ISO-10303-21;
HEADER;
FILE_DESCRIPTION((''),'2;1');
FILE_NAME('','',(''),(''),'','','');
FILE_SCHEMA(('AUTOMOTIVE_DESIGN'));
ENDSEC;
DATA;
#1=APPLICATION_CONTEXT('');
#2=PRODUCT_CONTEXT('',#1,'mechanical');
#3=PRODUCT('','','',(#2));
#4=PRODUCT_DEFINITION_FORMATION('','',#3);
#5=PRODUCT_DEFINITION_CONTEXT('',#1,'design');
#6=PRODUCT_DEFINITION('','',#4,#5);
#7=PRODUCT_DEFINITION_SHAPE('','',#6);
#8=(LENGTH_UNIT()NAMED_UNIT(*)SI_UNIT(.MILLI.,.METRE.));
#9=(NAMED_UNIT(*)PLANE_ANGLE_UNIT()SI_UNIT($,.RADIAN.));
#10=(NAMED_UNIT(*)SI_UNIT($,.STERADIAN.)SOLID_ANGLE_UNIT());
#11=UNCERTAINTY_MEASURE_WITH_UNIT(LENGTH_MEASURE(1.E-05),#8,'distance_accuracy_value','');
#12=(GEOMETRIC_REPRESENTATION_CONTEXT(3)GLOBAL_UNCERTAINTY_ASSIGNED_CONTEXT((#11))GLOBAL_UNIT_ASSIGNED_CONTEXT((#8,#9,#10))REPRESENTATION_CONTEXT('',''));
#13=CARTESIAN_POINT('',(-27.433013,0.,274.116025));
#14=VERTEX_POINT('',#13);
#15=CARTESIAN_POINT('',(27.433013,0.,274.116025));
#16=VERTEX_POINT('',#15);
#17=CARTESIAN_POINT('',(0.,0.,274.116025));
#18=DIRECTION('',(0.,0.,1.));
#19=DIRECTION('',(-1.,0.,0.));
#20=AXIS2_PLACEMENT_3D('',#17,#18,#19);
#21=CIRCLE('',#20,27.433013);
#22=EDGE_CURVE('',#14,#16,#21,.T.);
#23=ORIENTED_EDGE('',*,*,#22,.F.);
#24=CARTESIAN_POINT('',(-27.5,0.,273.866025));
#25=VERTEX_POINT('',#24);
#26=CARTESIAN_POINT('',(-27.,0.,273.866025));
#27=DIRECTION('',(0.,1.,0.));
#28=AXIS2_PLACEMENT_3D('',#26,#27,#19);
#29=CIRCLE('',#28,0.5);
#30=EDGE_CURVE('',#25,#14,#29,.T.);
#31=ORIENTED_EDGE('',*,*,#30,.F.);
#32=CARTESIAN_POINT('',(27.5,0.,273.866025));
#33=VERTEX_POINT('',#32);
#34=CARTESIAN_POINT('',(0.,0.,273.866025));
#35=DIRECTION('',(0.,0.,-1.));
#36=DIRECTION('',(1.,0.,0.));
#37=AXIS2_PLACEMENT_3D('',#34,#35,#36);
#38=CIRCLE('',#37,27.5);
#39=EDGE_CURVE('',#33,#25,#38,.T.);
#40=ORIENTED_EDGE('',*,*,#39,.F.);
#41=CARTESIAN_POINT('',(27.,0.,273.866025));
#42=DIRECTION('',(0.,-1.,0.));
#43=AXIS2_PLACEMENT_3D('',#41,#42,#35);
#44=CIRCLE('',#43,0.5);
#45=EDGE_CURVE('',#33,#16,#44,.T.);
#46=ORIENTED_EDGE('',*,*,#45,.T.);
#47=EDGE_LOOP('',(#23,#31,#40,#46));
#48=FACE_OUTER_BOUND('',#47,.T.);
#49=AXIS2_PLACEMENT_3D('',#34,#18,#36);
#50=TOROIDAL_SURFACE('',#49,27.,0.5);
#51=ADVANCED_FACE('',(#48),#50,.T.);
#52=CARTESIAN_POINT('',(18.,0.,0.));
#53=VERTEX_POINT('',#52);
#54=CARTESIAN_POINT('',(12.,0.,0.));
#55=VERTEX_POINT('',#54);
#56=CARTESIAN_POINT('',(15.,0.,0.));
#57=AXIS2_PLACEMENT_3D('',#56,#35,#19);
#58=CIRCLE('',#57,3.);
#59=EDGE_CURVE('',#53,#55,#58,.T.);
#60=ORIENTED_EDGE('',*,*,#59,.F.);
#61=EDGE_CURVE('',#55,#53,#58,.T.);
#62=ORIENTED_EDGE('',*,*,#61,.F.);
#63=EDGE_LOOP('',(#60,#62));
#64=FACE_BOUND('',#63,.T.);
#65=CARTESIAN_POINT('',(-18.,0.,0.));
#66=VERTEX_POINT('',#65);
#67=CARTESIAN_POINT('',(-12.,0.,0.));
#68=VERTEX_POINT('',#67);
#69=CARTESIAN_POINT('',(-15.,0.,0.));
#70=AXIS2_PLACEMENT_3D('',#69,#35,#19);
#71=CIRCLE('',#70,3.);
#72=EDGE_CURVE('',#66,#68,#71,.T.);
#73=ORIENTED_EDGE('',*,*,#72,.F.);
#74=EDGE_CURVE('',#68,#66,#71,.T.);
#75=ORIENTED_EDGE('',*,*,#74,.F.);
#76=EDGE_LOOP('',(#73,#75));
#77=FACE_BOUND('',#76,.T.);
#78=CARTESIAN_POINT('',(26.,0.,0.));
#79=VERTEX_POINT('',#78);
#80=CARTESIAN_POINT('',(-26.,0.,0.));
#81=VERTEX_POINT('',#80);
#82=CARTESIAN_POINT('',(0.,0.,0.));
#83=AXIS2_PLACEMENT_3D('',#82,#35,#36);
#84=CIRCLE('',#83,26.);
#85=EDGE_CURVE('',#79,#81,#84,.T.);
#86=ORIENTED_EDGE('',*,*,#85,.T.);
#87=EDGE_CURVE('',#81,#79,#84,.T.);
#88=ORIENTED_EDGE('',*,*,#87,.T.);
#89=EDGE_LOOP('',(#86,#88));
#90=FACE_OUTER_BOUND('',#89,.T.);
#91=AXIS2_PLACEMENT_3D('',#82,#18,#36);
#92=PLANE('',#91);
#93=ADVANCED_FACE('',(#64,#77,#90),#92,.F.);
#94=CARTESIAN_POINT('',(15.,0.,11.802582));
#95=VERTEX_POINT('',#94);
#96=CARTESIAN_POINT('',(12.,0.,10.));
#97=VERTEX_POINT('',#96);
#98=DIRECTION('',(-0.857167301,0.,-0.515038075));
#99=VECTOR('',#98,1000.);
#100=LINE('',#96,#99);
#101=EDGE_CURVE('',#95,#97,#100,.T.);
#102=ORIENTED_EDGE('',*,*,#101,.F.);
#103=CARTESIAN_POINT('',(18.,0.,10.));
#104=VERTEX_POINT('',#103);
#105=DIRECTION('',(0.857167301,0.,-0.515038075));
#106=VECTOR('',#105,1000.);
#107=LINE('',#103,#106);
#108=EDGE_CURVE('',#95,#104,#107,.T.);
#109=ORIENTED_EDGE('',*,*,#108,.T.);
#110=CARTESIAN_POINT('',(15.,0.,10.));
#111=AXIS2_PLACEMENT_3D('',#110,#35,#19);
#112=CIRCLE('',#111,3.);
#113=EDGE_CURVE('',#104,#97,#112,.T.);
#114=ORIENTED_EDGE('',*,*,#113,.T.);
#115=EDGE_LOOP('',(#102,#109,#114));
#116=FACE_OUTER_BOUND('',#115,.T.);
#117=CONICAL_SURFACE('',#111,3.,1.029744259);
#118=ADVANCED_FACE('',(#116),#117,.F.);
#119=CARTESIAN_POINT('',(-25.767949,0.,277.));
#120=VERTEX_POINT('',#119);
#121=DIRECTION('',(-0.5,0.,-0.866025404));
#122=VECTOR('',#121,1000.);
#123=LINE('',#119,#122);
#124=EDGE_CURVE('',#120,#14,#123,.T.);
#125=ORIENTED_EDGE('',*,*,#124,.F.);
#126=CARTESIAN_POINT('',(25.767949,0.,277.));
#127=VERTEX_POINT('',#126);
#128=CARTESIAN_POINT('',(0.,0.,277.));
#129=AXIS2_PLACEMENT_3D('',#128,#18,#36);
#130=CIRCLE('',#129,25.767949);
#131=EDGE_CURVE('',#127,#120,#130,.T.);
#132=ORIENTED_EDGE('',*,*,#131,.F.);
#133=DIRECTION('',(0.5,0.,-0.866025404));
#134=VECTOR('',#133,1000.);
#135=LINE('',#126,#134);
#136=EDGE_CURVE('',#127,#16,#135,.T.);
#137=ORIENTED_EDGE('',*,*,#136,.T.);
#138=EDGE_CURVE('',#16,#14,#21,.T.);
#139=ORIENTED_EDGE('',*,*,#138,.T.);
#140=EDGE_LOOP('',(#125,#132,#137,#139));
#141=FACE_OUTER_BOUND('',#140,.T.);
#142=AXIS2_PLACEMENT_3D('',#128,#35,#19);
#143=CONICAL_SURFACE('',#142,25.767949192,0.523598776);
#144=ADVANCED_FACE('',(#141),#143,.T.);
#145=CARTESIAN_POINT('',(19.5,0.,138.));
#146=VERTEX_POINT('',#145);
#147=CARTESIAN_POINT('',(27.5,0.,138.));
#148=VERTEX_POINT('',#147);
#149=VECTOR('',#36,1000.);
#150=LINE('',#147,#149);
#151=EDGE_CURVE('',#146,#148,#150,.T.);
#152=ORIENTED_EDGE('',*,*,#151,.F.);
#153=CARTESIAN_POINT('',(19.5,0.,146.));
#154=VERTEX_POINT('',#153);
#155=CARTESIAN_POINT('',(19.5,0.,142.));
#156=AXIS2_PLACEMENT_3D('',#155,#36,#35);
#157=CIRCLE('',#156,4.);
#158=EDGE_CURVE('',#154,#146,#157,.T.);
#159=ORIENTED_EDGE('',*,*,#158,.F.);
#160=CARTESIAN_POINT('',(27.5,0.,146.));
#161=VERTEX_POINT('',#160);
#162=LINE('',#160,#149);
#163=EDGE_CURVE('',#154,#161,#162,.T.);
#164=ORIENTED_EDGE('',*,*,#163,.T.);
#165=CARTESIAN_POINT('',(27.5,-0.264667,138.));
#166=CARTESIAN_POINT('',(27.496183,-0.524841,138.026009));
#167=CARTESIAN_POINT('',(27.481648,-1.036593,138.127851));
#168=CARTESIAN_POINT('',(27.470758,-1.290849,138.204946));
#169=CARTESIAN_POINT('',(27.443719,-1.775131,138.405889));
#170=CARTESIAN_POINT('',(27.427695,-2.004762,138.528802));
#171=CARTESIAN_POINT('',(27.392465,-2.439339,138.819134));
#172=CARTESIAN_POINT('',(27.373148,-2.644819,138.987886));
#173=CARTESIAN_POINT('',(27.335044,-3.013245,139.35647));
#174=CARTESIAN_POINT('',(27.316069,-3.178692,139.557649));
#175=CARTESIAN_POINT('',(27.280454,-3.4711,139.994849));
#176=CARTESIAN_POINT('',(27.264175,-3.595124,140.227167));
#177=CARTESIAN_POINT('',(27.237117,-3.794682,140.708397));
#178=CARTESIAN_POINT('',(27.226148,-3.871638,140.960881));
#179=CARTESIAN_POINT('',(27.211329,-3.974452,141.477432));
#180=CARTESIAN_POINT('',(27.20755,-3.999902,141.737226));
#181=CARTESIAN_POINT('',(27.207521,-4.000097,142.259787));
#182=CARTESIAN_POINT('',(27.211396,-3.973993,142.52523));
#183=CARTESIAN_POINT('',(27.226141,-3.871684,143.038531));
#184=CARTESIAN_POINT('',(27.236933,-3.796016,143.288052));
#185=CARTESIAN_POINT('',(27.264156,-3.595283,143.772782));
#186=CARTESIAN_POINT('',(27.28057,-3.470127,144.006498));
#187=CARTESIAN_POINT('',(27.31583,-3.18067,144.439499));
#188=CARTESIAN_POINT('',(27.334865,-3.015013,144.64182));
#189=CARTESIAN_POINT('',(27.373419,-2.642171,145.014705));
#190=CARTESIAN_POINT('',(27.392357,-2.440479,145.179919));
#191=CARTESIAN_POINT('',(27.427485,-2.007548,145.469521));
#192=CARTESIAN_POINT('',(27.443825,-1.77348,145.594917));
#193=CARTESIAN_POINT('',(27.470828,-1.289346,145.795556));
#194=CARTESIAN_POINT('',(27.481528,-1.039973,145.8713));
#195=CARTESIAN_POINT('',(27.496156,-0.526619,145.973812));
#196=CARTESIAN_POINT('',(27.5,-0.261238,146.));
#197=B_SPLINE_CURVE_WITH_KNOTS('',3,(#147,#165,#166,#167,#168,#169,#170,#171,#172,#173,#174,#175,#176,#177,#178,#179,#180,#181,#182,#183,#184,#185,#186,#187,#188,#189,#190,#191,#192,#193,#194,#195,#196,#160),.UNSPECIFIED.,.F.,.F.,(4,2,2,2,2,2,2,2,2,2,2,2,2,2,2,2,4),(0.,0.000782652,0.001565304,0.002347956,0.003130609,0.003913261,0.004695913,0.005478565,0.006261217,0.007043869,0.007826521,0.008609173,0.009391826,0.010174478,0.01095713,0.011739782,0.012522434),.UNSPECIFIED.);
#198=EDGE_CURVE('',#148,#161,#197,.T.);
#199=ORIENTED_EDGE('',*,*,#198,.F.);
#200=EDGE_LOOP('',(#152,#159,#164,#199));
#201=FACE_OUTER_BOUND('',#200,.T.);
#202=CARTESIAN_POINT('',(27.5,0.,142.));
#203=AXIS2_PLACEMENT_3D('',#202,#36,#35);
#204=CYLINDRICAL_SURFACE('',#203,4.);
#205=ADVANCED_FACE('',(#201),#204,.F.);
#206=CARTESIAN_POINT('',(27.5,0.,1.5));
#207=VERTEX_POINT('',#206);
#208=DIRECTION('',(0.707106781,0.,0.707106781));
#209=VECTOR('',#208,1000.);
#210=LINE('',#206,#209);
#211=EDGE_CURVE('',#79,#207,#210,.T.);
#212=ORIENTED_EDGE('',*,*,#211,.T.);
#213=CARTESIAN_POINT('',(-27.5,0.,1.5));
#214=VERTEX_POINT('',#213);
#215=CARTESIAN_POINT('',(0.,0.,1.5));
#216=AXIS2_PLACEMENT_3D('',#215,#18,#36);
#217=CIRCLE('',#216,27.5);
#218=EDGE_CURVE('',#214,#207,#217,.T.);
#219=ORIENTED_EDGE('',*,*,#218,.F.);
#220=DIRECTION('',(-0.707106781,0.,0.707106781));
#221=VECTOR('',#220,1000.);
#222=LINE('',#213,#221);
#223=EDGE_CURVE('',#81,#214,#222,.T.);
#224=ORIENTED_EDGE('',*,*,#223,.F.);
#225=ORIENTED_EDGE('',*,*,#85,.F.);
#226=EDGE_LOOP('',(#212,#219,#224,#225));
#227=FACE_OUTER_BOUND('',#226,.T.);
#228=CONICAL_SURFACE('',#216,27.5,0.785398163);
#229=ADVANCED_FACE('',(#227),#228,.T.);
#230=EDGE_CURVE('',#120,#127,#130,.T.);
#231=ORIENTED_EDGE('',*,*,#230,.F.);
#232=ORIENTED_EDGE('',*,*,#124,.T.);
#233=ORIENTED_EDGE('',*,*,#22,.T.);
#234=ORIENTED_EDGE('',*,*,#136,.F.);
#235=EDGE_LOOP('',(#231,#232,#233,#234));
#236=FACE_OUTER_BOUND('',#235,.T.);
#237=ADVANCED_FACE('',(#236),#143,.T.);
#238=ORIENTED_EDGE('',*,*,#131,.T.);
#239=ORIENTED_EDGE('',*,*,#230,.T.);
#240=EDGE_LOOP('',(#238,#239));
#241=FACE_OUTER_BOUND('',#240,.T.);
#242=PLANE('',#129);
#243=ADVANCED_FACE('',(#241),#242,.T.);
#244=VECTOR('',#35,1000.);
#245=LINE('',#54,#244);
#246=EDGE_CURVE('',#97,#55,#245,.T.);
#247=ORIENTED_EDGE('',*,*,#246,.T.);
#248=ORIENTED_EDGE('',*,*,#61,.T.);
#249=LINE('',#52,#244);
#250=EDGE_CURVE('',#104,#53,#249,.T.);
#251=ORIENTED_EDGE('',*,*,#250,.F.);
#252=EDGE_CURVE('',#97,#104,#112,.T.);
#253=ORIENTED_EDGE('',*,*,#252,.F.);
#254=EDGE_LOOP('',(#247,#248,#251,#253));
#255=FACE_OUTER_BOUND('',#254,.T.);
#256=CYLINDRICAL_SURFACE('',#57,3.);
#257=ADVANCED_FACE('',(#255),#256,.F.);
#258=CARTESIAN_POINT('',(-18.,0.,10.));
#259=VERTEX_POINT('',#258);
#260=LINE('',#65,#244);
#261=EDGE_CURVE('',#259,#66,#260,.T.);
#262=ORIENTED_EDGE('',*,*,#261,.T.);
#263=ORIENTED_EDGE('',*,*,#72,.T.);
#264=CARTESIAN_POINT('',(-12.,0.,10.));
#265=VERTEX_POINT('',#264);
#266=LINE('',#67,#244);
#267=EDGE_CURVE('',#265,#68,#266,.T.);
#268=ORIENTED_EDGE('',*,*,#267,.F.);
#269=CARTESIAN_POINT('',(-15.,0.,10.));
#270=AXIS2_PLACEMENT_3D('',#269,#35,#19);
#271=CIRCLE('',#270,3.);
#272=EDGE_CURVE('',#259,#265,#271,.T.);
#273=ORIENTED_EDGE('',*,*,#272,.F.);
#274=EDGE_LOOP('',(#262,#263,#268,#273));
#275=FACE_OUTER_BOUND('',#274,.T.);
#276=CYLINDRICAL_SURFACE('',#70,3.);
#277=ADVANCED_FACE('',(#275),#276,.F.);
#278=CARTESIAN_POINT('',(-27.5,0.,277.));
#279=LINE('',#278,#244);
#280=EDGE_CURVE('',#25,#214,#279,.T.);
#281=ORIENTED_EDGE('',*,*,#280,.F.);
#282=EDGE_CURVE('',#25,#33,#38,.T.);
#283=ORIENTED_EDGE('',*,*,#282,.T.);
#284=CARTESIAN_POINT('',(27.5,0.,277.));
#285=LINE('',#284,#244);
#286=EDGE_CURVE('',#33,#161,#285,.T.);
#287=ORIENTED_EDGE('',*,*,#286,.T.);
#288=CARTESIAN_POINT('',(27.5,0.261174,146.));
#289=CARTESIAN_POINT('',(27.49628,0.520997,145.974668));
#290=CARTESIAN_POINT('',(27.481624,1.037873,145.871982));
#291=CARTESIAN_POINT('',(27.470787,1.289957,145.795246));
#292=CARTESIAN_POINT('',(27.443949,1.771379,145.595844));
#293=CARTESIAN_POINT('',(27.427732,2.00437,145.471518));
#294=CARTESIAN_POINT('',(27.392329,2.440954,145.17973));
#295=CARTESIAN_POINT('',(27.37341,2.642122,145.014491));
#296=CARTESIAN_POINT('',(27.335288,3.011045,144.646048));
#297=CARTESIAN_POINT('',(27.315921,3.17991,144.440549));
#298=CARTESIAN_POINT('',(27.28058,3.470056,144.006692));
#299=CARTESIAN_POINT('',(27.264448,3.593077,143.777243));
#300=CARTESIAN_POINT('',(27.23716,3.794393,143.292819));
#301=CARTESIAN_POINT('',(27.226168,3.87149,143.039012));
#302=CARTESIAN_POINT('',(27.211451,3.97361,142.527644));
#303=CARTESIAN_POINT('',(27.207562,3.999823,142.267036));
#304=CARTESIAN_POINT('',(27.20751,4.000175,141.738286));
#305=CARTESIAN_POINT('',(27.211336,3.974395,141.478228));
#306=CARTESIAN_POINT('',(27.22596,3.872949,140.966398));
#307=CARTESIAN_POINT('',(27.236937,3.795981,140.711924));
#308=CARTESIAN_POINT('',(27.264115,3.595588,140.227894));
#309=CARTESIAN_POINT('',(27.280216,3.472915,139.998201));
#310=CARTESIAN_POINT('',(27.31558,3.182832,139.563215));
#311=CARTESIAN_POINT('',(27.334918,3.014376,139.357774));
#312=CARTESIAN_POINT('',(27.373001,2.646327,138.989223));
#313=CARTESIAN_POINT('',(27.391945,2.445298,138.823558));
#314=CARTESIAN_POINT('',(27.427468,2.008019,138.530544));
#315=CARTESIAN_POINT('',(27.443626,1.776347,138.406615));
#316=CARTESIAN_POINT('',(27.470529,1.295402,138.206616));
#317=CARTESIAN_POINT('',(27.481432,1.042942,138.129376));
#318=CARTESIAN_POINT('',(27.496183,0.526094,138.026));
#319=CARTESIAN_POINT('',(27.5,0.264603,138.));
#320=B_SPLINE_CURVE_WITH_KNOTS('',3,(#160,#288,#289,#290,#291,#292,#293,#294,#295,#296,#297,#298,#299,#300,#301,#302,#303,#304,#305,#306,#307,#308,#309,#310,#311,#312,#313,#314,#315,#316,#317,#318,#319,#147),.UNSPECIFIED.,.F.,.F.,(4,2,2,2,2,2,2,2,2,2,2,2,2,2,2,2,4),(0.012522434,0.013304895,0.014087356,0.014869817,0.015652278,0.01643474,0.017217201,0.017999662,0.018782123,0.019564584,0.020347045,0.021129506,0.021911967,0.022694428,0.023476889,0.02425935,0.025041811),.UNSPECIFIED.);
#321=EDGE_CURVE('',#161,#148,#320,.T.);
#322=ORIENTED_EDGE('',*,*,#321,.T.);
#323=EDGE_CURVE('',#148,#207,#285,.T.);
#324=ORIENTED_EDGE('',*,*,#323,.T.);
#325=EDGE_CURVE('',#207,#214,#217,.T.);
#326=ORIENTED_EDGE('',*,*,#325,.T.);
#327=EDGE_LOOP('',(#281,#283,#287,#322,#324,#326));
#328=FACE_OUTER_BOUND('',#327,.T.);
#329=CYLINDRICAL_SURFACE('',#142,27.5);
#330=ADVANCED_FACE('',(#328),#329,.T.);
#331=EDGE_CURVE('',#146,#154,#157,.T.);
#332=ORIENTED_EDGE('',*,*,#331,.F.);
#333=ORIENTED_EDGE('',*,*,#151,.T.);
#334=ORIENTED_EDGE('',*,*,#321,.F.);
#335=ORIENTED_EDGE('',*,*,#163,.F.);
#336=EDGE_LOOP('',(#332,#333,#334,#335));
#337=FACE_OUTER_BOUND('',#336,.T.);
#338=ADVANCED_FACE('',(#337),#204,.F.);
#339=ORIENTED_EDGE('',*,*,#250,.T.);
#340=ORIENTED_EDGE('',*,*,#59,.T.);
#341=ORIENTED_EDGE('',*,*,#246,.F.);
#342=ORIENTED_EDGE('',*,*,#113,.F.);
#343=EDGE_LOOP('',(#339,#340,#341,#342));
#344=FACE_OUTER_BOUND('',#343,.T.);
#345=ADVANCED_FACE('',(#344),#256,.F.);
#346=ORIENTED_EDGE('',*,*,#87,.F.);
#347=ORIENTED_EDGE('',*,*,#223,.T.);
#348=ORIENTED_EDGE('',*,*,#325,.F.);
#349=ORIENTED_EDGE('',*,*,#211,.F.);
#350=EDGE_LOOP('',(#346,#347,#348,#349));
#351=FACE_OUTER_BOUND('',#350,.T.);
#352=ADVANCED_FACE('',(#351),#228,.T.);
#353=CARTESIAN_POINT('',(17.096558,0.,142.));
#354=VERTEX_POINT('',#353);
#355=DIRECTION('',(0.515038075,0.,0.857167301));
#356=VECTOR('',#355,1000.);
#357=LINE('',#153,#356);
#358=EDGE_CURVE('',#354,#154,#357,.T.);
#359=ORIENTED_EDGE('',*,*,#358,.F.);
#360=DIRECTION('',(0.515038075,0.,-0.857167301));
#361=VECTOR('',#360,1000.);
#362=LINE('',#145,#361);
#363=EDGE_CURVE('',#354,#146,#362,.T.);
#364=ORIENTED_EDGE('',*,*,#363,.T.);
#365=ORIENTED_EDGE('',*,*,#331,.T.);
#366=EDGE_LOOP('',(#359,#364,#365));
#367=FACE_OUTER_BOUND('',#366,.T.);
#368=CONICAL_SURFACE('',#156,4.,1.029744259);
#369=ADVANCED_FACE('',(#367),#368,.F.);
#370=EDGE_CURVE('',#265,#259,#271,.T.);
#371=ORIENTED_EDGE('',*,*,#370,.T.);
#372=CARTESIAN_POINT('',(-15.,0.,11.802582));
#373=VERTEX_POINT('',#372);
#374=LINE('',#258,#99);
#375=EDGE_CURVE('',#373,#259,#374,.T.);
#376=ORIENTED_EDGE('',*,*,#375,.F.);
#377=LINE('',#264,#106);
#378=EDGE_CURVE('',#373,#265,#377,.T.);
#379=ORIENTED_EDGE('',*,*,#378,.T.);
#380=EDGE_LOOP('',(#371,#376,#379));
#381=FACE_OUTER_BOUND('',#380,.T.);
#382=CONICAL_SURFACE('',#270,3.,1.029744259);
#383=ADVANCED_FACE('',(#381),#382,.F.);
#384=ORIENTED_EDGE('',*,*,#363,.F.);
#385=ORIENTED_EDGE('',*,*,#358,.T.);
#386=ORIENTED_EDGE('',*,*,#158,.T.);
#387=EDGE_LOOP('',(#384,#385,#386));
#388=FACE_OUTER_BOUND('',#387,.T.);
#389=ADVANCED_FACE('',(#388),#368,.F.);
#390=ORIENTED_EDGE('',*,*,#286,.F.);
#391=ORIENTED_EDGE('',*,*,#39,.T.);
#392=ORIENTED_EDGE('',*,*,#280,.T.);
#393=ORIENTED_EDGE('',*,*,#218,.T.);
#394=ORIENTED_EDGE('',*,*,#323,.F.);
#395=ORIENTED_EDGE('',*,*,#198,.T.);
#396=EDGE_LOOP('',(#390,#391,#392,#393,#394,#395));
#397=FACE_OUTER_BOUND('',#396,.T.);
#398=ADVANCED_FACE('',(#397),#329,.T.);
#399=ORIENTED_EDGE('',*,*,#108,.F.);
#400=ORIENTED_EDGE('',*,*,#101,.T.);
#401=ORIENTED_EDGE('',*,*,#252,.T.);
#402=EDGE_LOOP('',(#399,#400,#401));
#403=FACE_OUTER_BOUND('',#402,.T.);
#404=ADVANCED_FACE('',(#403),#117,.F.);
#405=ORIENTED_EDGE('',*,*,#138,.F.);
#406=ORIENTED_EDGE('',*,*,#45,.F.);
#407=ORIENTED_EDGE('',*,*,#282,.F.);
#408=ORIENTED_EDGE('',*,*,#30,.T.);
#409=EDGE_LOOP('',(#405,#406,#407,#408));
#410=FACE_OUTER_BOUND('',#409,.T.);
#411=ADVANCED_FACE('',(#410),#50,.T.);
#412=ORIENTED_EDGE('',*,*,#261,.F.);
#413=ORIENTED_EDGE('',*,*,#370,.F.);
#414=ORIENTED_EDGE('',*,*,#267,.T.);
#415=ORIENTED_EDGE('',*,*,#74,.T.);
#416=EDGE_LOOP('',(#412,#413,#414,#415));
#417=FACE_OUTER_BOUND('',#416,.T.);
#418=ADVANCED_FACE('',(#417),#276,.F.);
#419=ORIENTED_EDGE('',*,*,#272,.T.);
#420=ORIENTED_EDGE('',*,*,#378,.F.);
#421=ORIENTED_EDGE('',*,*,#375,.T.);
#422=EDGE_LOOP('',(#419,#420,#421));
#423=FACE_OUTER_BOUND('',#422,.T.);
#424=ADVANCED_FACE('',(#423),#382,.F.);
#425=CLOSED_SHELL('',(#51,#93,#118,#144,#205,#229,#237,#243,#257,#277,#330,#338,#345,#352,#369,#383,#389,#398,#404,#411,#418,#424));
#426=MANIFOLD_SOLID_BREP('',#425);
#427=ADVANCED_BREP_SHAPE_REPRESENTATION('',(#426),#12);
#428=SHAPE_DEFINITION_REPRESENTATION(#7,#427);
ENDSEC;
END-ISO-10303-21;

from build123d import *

# Parameters (mm, degrees)
SKETCH_1_R      = 27.5
EXTRUDE_1_DEPTH = 277
MM_1_D          = 6
MM_1_DEPTH      = 10
MM_1_TIP        = 1.802581857
MM_2_D          = 8
MM_2_DEPTH      = 8
MM_2_TIP        = 2.403442476
CHAMFER_1_SIZE  = 1.5
CHAMFER_2_SIZE  = 3
CHAMFER_2_SIZE2 = 1.732050808
FILLET_1_R      = 0.5


with BuildPart() as part:
    # 草图1 → 凸台-拉伸1 (new body)
    with BuildSketch(Plane.XY):
        Circle(SKETCH_1_R)
    extrude(amount=EXTRUDE_1_DEPTH)

    # 大小mm 暗销孔1
    with Locations(Plane(origin=(0, 0, 0), x_dir=(1, 0, 0), z_dir=(0, 0, -1))):
        with Locations((15, 0), (-15, 0)):
            Hole(MM_1_D / 2, depth=MM_1_DEPTH)
            with Locations((0, 0, -(MM_1_DEPTH + MM_1_TIP / 2))):  # 118° drill point
                Cone(0, MM_1_D / 2, MM_1_TIP, mode=Mode.SUBTRACT)

    # 大小mm 暗销孔2
    with Locations(Plane(origin=(27.5, 0, 0), x_dir=(0, 0, -1), z_dir=(1, 0, 0))):
        with Locations((-142, 0)):
            Hole(MM_2_D / 2, depth=MM_2_DEPTH)
            with Locations((0, 0, -(MM_2_DEPTH + MM_2_TIP / 2))):  # 118° drill point
                Cone(0, MM_2_D / 2, MM_2_TIP, mode=Mode.SUBTRACT)

    # 倒角1
    chamfer_1_edges = [part.edges().sort_by_distance(p)[0] for p in [
        (-27.5, 0, 0),
    ]]
    chamfer(chamfer_1_edges, length=CHAMFER_1_SIZE)

    # 倒角2
    chamfer_2_edges = [part.edges().sort_by_distance(p)[0] for p in [
        (-27.5, 0, 277),
    ]]
    chamfer_2_side = [part.faces().sort_by_distance(p)[0] for p in [
        (-27.5, 0, 139.25),
    ]]
    chamfer(chamfer_2_edges, length=CHAMFER_2_SIZE, length2=CHAMFER_2_SIZE2, reference=chamfer_2_side[0])

    # 圆角1
    fillet_1_edges = [part.edges().sort_by_distance(p)[0] for p in [
        (-27.5, 0, 274),
    ]]
    fillet(fillet_1_edges, radius=FILLET_1_R)


solid = part.part
